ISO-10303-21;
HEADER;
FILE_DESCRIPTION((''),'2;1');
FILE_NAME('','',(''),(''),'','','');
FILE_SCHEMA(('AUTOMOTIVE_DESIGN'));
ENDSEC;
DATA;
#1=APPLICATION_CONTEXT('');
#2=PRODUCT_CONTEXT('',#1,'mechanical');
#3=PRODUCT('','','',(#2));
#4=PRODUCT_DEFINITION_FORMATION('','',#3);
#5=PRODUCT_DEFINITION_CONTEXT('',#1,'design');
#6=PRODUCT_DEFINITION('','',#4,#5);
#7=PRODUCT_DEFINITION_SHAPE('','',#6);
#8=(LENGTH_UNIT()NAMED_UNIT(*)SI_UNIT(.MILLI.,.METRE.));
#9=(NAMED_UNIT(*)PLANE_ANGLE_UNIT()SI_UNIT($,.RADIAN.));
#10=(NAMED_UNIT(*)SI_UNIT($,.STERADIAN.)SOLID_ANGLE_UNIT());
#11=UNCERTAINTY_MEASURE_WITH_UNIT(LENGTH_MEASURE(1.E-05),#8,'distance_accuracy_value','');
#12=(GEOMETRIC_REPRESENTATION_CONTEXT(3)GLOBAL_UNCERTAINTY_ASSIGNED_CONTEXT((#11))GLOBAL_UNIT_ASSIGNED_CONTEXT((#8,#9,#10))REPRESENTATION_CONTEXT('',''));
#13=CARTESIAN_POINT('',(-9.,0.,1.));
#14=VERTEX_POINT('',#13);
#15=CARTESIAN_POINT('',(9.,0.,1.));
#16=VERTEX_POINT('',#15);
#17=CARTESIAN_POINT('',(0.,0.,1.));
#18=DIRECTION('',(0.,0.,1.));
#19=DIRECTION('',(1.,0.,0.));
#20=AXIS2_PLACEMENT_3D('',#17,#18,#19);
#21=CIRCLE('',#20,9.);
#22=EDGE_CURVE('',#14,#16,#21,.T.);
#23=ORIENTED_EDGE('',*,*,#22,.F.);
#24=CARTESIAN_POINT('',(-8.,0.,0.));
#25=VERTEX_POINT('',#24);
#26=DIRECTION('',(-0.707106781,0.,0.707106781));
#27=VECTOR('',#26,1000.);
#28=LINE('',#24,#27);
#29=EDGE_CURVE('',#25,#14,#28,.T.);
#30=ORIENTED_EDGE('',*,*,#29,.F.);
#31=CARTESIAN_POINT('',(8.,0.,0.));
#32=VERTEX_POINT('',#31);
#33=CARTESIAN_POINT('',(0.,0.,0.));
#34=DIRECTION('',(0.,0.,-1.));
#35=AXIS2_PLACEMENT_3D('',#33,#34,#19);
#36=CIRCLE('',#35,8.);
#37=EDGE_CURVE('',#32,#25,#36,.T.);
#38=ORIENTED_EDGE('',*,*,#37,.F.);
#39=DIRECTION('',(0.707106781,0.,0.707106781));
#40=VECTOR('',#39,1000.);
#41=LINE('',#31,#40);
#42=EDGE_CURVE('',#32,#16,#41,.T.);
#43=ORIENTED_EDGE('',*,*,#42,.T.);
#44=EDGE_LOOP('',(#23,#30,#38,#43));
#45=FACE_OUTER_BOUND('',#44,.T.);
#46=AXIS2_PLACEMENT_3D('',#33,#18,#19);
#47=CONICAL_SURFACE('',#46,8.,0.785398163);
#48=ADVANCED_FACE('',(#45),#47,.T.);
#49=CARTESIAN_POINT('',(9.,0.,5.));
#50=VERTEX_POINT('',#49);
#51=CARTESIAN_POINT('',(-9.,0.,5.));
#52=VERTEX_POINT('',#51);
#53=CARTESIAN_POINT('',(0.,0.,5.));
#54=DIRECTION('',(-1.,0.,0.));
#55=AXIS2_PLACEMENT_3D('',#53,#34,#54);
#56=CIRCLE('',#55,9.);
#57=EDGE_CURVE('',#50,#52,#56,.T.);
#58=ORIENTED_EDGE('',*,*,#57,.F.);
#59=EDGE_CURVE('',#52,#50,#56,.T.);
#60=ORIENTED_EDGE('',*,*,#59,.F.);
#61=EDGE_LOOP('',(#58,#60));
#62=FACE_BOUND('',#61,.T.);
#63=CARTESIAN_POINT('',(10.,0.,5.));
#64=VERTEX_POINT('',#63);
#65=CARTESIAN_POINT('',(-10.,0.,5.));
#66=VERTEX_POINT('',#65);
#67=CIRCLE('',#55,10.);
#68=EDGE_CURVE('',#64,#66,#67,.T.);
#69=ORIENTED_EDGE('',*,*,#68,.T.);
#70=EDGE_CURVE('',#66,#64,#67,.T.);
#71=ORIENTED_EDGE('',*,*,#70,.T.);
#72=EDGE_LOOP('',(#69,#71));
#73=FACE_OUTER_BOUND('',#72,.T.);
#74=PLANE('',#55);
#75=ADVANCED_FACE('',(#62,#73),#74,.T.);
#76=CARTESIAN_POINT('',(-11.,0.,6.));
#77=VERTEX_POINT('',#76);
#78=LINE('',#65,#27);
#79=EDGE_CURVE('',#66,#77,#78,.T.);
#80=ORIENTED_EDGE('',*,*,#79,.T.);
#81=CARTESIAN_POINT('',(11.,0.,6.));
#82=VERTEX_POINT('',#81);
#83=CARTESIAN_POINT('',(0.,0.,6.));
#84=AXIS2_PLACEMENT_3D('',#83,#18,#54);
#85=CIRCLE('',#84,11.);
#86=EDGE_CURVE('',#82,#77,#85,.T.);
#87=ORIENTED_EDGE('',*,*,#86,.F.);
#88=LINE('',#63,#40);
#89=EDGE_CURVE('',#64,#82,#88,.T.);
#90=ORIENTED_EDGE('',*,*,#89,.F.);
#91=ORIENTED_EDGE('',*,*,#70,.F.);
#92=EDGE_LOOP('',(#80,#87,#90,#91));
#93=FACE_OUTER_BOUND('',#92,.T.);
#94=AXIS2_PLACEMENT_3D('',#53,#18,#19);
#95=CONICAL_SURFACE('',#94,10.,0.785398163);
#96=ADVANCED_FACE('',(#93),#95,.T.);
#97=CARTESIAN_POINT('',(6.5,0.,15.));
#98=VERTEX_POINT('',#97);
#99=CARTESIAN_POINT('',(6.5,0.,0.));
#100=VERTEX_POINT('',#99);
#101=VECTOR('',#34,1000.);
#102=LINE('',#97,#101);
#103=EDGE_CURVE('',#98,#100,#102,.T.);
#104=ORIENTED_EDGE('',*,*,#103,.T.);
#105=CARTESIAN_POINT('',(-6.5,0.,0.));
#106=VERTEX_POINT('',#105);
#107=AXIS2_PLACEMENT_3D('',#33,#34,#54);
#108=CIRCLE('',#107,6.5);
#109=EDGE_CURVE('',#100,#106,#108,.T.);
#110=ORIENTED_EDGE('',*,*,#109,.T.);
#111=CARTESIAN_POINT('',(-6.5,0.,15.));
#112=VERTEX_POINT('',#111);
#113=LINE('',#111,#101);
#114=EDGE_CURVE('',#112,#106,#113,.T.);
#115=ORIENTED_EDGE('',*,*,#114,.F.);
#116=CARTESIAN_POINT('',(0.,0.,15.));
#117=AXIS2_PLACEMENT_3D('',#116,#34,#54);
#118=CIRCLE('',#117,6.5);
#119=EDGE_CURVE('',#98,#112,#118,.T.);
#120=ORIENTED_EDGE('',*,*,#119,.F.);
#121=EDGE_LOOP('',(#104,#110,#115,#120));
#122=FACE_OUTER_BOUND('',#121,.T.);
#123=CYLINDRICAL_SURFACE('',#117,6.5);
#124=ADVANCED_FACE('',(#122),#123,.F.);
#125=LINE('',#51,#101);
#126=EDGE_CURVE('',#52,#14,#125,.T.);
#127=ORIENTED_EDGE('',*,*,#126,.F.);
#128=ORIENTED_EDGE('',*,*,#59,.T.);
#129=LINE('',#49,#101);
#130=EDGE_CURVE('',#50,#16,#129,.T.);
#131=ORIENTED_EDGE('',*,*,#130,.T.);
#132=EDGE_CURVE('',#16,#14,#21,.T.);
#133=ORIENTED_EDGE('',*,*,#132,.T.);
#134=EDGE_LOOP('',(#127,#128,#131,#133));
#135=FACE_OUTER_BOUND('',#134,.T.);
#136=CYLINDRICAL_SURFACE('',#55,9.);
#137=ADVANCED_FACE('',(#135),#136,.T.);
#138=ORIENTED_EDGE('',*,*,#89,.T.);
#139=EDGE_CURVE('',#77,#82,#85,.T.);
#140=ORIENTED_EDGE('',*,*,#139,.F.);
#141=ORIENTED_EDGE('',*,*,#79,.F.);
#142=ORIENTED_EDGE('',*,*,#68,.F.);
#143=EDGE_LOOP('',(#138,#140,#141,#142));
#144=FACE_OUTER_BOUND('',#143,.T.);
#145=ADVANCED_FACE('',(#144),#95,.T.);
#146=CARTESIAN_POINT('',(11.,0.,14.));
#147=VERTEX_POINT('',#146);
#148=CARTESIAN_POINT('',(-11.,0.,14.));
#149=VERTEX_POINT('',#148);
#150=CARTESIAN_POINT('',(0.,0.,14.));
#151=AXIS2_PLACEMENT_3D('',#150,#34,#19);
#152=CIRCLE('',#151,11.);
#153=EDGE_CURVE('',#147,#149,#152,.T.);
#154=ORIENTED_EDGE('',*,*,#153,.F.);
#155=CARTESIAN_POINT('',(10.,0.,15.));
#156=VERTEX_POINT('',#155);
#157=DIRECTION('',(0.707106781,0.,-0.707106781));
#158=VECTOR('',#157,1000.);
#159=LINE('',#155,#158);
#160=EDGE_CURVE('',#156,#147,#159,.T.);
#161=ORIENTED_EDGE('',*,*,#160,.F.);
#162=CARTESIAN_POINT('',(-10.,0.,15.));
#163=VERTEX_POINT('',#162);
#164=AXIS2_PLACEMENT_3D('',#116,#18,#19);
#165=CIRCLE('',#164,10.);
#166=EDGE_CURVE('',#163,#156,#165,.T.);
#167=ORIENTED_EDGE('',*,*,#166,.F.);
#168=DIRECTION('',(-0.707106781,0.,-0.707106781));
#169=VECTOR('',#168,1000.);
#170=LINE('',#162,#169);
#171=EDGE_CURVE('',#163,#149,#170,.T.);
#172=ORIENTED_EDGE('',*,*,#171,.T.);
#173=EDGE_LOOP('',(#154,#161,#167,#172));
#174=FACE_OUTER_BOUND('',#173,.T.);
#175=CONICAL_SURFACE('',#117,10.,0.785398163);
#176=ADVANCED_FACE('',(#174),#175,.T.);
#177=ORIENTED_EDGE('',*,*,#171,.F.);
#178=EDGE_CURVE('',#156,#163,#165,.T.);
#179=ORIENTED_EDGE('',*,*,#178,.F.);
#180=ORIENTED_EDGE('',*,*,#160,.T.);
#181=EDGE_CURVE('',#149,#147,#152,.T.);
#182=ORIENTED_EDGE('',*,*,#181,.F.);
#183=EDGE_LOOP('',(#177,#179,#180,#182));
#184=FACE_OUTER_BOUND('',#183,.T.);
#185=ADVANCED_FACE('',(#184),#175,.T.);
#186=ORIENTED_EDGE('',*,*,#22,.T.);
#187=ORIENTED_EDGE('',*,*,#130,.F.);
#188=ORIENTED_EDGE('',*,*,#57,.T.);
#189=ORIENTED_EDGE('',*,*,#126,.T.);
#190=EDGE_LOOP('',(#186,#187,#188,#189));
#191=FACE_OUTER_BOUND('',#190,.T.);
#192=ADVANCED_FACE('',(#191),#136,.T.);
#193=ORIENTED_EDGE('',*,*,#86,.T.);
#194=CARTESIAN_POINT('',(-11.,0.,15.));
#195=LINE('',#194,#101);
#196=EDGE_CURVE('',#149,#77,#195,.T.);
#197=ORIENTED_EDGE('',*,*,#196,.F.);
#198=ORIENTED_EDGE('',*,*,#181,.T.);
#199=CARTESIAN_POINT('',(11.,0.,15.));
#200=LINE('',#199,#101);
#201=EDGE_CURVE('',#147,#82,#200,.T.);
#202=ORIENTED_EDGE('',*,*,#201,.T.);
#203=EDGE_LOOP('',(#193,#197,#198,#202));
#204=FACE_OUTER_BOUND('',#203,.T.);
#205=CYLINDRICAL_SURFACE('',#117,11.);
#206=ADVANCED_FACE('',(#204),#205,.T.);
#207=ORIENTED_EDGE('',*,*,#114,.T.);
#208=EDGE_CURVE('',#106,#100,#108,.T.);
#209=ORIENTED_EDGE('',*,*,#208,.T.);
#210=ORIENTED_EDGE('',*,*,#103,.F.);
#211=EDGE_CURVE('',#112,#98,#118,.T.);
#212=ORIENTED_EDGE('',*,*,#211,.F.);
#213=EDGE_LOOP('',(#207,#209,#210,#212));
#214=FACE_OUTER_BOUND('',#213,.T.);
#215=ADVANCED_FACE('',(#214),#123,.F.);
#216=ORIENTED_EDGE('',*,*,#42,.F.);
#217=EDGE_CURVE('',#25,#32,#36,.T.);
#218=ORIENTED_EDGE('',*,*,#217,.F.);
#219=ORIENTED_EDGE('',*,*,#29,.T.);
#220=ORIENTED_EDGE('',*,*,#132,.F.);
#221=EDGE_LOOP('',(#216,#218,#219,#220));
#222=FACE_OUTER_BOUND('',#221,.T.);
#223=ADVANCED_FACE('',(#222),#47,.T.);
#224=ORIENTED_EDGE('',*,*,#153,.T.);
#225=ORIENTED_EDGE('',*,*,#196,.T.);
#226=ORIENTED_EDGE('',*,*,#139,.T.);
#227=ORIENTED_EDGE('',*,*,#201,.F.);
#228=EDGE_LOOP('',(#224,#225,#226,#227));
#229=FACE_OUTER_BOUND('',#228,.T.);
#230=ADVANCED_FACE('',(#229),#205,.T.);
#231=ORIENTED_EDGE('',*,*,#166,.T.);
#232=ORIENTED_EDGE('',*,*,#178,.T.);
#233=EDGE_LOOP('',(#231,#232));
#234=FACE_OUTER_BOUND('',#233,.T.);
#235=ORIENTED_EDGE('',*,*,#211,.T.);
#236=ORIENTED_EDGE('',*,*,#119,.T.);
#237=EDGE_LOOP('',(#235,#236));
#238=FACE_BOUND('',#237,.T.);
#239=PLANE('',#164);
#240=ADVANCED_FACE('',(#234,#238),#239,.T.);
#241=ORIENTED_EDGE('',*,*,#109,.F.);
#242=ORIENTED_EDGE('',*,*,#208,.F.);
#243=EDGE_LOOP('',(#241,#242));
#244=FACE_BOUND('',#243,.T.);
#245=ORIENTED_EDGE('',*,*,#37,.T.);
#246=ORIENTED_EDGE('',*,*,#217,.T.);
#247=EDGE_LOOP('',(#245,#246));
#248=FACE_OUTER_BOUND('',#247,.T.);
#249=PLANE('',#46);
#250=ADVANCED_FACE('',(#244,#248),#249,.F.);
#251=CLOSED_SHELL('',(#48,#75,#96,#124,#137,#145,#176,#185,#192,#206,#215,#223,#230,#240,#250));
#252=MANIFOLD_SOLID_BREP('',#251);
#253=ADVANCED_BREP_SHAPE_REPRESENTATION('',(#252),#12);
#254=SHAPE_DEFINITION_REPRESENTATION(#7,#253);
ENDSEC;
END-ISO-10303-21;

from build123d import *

# Parameters (mm, degrees)
SKETCH1_R           = 11
BOSS_EXTRUDE1_DEPTH = 15
SKETCH2_R           = 11
SKETCH2_R_2         = 9
CUT_EXTRUDE1_DEPTH  = 5
SKETCH3_R           = 6.5
CUT_EXTRUDE2_DEPTH  = 22.610182785
CHAMFER1_SIZE       = 1


with BuildPart() as part:
    # Sketch1 → Boss-Extrude1 (new body)
    with BuildSketch(Plane.XY):
        Circle(SKETCH1_R)
    extrude(amount=BOSS_EXTRUDE1_DEPTH)

    # Sketch2 → Cut-Extrude1 (cut)
    with BuildSketch(Plane(origin=(0, 0, 0), x_dir=(-1, 0, 0), z_dir=(0, 0, -1))):
        Circle(SKETCH2_R)
        Circle(SKETCH2_R_2, mode=Mode.SUBTRACT)
    extrude(amount=-CUT_EXTRUDE1_DEPTH, mode=Mode.SUBTRACT)

    # Sketch3 → Cut-Extrude2 (cut, through all)
    with BuildSketch(Plane(origin=(0, 0, 0), x_dir=(-1, 0, 0), z_dir=(0, 0, -1))):
        Circle(SKETCH3_R)
    extrude(amount=-CUT_EXTRUDE2_DEPTH, mode=Mode.SUBTRACT)

    # Chamfer1
    chamfer1_edges = [part.edges().sort_by_distance(p)[0] for p in [
        (-11, 0, 15),
        (-11, 0, 5),
        (9, 0, 0),
    ]]
    chamfer(chamfer1_edges, length=CHAMFER1_SIZE)


solid = part.part
